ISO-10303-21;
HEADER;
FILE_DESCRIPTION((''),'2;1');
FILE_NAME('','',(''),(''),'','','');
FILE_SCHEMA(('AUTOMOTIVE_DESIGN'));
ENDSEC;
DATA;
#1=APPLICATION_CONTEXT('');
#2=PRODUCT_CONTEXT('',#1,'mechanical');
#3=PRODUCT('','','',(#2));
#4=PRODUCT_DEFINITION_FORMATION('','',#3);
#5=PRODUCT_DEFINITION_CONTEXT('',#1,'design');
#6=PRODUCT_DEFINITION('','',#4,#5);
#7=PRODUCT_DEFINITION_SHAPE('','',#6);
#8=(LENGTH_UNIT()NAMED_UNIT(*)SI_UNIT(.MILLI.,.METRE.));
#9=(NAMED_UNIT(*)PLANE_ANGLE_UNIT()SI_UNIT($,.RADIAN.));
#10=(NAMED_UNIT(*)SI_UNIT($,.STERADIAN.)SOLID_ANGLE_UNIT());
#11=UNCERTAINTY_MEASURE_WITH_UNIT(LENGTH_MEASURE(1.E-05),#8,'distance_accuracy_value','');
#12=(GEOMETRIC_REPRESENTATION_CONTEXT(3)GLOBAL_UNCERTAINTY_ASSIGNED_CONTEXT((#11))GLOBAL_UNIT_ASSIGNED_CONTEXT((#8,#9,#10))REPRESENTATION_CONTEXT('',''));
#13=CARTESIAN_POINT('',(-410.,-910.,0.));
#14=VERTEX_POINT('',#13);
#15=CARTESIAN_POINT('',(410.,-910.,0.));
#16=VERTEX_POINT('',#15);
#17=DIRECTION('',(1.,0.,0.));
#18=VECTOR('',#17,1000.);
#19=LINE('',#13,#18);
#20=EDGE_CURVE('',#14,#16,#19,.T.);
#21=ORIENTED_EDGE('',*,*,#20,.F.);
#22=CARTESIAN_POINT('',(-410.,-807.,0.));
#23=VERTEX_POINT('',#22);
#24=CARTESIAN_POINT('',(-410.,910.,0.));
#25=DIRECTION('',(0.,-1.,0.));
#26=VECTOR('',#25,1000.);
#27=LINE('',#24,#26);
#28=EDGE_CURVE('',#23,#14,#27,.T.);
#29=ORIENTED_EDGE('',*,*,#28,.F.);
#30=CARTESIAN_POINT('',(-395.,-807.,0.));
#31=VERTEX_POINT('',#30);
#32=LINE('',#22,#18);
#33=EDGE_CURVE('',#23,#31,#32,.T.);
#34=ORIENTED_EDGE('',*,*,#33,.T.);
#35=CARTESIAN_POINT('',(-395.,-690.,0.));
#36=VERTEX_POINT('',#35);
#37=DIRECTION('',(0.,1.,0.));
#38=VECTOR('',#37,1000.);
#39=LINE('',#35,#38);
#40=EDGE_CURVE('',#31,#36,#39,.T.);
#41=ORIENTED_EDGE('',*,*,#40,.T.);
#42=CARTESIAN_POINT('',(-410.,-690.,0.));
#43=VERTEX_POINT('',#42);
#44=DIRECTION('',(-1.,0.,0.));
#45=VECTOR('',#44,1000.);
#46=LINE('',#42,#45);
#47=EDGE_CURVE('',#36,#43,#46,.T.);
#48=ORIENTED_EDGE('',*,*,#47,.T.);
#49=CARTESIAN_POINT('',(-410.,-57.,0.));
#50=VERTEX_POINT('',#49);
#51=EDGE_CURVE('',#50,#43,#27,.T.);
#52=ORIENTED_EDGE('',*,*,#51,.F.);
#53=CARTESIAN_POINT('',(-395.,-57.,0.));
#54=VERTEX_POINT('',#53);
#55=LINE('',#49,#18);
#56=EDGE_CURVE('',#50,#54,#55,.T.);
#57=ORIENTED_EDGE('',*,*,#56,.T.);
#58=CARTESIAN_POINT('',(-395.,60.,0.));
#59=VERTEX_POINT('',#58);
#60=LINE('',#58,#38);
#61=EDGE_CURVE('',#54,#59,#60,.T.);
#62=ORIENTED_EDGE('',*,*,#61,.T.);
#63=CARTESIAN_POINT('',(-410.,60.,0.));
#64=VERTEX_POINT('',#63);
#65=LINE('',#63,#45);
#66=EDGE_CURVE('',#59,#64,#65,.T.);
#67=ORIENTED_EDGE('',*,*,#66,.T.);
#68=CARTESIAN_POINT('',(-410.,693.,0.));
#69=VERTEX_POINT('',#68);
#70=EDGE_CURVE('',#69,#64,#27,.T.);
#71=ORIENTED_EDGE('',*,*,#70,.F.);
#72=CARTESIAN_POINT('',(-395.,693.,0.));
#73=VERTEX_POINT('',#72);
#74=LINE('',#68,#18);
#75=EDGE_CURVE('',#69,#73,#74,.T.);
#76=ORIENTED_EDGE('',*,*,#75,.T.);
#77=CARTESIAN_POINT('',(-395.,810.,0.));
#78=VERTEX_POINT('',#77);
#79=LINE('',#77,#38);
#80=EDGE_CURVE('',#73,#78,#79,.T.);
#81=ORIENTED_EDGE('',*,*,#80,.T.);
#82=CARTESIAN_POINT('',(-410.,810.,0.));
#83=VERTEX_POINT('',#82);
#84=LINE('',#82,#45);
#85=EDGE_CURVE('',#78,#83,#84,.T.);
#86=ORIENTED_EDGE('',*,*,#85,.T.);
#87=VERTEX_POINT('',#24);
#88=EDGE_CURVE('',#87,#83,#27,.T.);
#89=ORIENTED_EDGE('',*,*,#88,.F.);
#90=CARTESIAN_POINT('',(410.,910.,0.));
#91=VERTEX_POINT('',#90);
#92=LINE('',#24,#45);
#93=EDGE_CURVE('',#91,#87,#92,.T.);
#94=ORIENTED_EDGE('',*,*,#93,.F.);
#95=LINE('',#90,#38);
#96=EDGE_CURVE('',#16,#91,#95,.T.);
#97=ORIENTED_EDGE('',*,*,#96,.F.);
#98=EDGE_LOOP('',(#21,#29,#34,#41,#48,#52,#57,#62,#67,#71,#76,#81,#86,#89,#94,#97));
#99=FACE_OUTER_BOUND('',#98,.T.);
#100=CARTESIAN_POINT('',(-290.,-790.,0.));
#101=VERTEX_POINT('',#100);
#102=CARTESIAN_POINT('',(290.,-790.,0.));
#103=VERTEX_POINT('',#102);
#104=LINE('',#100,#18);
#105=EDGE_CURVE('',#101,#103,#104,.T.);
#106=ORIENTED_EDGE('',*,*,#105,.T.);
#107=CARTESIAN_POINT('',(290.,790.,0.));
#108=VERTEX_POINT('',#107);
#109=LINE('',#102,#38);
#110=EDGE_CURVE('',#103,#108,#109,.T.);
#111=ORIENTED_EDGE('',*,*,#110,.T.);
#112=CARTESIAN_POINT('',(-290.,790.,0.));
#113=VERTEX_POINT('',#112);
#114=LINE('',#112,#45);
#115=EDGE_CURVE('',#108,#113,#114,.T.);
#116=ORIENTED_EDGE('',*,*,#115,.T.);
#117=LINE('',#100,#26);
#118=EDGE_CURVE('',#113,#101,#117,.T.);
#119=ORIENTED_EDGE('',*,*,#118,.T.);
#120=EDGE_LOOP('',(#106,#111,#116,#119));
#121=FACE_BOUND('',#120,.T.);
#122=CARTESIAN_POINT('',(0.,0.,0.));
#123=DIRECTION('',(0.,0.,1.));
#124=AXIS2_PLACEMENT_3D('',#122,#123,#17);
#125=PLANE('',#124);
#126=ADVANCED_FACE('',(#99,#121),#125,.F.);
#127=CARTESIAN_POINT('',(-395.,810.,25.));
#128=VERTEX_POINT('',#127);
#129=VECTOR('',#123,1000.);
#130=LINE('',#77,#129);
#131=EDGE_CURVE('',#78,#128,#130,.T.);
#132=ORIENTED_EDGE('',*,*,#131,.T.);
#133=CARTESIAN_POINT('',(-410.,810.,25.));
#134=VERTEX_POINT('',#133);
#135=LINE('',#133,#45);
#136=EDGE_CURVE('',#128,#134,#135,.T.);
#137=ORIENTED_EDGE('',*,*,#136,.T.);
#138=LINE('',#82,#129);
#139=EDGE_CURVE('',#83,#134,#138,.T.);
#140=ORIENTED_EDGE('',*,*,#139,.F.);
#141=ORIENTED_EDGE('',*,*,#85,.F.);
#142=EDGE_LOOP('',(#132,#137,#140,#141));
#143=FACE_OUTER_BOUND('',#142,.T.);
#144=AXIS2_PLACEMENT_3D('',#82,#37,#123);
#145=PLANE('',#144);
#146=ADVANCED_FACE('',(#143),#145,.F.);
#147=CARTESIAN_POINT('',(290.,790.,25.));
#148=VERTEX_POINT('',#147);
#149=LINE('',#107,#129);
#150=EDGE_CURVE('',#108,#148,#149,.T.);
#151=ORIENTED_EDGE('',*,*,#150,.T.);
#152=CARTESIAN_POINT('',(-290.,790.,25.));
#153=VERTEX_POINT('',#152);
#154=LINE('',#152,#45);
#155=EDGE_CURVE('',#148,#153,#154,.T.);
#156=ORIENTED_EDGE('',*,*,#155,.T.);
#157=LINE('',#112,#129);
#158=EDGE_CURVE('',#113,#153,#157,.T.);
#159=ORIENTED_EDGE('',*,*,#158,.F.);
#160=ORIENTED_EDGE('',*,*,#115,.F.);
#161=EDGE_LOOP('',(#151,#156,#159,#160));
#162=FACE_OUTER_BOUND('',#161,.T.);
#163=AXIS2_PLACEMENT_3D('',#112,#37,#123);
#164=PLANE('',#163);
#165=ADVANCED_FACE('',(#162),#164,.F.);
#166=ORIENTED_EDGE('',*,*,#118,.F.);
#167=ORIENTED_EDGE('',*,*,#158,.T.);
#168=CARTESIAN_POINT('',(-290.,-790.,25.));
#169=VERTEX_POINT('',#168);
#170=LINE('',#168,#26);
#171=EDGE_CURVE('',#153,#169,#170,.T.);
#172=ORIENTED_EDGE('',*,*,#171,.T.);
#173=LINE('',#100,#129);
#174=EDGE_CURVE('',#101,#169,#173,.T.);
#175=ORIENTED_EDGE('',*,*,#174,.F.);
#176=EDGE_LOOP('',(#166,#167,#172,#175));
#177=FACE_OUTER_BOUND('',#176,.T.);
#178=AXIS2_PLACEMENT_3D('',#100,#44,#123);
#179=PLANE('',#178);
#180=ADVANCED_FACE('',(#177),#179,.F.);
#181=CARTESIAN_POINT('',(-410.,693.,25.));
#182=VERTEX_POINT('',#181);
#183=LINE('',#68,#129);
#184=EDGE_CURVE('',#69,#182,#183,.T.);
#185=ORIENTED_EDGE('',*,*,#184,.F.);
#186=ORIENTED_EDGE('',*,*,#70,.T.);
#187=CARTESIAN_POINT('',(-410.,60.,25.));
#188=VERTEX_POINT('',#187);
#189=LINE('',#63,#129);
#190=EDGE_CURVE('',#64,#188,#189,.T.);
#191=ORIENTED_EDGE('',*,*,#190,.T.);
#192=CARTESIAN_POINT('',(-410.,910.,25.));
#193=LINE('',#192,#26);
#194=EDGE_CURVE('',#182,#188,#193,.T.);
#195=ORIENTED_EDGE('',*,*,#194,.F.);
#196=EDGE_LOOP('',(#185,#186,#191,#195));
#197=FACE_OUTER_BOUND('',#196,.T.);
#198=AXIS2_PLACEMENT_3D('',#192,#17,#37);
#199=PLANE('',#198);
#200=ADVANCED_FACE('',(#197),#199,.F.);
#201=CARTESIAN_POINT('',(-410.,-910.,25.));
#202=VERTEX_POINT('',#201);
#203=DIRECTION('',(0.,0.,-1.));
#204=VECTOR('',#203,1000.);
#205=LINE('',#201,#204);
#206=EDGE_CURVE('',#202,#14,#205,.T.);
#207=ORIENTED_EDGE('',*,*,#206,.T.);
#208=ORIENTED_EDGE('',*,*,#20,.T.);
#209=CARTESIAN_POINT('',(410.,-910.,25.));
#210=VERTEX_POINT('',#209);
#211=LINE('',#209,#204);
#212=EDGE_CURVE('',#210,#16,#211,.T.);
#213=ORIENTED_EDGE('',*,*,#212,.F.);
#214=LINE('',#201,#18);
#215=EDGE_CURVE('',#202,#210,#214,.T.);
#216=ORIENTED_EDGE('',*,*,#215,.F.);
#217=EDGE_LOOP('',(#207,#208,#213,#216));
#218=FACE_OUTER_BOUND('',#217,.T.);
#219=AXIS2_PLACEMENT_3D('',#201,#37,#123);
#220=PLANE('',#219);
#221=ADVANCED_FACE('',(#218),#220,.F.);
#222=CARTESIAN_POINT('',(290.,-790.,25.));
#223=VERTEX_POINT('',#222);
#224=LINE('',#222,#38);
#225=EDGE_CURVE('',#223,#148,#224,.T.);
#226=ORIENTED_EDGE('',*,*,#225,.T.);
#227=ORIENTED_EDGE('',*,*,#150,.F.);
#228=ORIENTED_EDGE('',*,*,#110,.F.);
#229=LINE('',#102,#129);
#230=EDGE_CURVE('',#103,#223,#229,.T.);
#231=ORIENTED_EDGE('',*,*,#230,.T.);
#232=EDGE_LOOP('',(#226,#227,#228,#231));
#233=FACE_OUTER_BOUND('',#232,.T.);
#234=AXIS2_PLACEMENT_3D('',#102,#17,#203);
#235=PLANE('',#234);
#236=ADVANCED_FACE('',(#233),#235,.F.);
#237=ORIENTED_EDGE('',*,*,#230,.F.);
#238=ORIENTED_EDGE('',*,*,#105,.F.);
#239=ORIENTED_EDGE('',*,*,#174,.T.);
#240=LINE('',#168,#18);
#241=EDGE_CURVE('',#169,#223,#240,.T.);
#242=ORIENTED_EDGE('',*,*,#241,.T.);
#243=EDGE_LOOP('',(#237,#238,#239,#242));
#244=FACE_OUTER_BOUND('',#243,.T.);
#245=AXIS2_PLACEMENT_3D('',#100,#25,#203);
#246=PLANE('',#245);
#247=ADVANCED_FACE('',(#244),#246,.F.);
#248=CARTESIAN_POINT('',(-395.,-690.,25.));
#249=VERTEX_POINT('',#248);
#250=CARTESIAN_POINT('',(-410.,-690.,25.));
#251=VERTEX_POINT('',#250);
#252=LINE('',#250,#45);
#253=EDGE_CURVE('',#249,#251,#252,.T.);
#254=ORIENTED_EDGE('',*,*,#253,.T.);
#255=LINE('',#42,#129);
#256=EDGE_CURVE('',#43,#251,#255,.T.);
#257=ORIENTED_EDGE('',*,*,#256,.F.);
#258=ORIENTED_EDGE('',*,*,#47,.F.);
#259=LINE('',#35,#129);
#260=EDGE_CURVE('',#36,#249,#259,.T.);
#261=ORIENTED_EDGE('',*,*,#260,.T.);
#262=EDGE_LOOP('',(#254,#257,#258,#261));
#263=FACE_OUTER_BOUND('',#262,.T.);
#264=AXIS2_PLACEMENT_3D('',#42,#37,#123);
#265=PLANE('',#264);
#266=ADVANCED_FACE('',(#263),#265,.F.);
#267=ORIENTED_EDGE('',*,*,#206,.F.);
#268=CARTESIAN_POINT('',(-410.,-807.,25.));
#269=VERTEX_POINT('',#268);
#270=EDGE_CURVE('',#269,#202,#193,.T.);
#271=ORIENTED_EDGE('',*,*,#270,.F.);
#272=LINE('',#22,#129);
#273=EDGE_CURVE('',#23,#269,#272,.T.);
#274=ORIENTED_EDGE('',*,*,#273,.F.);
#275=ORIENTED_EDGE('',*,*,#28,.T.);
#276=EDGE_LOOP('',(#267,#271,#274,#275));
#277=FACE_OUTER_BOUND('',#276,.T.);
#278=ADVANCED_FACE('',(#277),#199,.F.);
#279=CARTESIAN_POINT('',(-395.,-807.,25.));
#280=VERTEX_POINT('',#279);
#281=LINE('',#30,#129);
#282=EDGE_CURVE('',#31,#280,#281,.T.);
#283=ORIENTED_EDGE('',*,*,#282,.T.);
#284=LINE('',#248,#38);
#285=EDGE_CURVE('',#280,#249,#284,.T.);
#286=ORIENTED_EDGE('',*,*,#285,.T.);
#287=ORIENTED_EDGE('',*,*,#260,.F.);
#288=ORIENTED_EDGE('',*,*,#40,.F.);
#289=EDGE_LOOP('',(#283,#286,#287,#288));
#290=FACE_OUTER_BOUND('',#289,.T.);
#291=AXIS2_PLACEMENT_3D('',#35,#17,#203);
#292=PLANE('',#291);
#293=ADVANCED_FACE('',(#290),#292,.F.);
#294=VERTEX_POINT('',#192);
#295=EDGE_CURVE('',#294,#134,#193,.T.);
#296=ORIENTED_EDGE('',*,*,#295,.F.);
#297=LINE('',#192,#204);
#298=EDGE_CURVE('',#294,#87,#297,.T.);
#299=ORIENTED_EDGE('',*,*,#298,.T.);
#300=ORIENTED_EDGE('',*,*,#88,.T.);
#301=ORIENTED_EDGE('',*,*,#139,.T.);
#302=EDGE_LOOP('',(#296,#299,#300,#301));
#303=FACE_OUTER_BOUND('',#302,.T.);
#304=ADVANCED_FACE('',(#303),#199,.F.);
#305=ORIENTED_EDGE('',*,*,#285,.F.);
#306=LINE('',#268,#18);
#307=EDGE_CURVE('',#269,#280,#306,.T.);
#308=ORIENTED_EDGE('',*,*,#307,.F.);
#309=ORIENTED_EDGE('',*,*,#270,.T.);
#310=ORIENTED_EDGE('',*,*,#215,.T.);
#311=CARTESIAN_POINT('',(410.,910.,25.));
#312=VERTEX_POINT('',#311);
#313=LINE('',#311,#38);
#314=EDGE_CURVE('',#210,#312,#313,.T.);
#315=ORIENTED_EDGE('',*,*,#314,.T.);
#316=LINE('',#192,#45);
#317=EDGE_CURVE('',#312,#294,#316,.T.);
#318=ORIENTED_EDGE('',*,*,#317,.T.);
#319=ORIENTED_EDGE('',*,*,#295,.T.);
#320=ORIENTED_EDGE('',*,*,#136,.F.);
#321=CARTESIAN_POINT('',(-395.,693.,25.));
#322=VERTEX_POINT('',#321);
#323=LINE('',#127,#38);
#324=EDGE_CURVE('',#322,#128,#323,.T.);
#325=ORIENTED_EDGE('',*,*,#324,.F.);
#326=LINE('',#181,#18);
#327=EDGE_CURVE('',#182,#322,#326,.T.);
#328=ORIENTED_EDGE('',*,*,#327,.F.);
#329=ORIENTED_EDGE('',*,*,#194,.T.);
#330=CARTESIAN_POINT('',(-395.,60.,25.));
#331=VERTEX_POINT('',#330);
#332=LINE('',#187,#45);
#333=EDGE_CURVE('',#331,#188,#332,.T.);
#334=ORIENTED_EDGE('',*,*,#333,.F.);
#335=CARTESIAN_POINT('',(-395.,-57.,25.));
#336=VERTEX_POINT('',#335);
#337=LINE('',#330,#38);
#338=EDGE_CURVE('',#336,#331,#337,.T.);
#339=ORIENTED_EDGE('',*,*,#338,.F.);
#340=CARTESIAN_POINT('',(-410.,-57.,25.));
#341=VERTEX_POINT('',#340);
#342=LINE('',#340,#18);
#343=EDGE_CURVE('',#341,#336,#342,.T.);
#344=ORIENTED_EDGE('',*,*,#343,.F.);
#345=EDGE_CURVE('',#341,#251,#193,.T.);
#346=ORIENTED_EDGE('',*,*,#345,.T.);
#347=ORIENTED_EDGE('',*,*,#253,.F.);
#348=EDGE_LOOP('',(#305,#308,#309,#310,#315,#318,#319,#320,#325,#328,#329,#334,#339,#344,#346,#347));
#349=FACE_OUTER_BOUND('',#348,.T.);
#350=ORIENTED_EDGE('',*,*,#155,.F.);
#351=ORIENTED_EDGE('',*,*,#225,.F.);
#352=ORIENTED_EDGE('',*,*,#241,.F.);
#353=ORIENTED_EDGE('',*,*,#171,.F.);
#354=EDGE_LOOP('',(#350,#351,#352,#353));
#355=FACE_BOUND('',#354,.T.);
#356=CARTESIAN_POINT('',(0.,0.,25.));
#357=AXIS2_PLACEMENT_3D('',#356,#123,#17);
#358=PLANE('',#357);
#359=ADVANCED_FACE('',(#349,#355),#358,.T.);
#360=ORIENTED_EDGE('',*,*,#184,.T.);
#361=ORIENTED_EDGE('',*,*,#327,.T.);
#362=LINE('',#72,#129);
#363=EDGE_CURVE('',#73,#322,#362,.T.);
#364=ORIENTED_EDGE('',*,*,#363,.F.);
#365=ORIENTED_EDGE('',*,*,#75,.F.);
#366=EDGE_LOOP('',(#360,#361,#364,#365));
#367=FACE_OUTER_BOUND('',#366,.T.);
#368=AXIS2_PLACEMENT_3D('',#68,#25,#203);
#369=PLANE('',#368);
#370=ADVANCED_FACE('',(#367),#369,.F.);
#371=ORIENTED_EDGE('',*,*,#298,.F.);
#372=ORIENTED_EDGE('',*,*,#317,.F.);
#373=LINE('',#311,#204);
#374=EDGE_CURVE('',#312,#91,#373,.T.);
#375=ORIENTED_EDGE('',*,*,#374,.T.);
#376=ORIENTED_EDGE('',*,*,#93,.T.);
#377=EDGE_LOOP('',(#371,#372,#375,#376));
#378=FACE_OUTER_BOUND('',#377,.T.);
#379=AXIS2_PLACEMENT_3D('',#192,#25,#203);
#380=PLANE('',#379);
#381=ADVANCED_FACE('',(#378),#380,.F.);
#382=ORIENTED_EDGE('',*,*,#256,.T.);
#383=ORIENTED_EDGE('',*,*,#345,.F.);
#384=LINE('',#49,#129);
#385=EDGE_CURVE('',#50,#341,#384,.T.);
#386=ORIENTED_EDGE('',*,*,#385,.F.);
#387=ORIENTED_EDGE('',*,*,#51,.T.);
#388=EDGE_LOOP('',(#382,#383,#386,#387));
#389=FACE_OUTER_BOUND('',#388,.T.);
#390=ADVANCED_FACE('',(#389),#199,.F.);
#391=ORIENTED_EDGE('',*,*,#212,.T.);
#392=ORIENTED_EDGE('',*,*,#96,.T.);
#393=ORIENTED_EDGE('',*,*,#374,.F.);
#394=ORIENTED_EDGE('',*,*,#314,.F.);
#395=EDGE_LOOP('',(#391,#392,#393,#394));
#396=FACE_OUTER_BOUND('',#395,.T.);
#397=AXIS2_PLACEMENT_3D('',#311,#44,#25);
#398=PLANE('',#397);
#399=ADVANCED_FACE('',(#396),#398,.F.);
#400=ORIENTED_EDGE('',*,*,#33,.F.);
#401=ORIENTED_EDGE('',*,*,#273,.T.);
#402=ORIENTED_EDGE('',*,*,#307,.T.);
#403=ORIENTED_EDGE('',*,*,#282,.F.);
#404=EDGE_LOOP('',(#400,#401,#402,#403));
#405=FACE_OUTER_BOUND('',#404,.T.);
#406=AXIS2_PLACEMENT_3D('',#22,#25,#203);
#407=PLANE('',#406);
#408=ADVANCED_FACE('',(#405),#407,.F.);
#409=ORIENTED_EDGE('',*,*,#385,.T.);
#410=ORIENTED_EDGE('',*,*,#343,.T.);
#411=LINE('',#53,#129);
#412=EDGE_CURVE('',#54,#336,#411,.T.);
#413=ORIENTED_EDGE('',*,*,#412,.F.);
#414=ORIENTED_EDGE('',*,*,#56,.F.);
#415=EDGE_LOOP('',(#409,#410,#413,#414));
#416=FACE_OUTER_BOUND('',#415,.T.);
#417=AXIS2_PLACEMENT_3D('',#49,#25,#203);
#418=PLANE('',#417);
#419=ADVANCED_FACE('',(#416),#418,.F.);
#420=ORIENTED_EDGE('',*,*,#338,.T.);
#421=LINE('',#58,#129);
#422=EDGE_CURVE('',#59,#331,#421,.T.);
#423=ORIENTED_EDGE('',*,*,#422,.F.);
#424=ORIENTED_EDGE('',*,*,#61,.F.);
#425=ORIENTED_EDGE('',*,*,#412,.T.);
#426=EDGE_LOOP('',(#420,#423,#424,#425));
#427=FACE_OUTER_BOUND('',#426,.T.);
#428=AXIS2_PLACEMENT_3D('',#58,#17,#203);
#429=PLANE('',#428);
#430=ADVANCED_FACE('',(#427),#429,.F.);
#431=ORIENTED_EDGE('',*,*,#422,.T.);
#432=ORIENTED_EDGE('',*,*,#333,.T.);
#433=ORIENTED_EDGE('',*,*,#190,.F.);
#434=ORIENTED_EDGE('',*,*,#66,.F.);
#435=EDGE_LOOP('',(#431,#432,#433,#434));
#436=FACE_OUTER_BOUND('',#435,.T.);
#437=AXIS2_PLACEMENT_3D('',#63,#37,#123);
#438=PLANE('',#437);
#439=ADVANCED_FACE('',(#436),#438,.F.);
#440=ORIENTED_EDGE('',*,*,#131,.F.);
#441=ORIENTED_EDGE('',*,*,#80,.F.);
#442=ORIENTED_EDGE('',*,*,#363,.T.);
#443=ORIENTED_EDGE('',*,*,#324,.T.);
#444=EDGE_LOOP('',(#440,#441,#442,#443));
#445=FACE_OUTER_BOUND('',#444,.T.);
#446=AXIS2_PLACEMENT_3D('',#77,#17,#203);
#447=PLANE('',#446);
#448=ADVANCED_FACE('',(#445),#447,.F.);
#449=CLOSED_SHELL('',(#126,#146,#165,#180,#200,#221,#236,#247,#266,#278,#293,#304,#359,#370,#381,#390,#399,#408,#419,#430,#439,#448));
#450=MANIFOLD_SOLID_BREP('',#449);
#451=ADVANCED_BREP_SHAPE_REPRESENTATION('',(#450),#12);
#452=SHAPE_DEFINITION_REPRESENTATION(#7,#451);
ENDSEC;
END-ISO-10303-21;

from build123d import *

# Parameters (mm, degrees)
SKETCH_1_W          = 820
SKETCH_1_H          = 1820
EXTRUDE_1_DEPTH     = 25
SKETCH_2_W          = 580
SKETCH_2_H          = 1580
CUT_EXTRUDE_1_DEPTH = 999.411237918
SKETCH_3_W          = 15
SKETCH_3_H          = 117
CUT_EXTRUDE_2_DEPTH = 999.411237918


with BuildPart() as part:
    # 草图1 → 凸台-拉伸1 (new body)
    with BuildSketch(Plane.XY):
        Rectangle(SKETCH_1_W, SKETCH_1_H)
    extrude(amount=EXTRUDE_1_DEPTH)

    # 草图2 → 切除-拉伸1 (cut, through all)
    with BuildSketch(Plane.XY.offset(25)):
        Rectangle(SKETCH_2_W, SKETCH_2_H)
    extrude(amount=-CUT_EXTRUDE_1_DEPTH, mode=Mode.SUBTRACT)

    # 草图3 → 切除-拉伸2 (cut, through all)
    with BuildSketch(Plane.XY.offset(25)):
        with Locations((-402.5, -748.5)):
            Rectangle(SKETCH_3_W, SKETCH_3_H)
        with Locations((-402.5, 1.5)):
            Rectangle(SKETCH_3_W, SKETCH_3_H)
        with Locations((-402.5, 751.5)):
            Rectangle(SKETCH_3_W, SKETCH_3_H)
    extrude(amount=-CUT_EXTRUDE_2_DEPTH, mode=Mode.SUBTRACT)


solid = part.part
